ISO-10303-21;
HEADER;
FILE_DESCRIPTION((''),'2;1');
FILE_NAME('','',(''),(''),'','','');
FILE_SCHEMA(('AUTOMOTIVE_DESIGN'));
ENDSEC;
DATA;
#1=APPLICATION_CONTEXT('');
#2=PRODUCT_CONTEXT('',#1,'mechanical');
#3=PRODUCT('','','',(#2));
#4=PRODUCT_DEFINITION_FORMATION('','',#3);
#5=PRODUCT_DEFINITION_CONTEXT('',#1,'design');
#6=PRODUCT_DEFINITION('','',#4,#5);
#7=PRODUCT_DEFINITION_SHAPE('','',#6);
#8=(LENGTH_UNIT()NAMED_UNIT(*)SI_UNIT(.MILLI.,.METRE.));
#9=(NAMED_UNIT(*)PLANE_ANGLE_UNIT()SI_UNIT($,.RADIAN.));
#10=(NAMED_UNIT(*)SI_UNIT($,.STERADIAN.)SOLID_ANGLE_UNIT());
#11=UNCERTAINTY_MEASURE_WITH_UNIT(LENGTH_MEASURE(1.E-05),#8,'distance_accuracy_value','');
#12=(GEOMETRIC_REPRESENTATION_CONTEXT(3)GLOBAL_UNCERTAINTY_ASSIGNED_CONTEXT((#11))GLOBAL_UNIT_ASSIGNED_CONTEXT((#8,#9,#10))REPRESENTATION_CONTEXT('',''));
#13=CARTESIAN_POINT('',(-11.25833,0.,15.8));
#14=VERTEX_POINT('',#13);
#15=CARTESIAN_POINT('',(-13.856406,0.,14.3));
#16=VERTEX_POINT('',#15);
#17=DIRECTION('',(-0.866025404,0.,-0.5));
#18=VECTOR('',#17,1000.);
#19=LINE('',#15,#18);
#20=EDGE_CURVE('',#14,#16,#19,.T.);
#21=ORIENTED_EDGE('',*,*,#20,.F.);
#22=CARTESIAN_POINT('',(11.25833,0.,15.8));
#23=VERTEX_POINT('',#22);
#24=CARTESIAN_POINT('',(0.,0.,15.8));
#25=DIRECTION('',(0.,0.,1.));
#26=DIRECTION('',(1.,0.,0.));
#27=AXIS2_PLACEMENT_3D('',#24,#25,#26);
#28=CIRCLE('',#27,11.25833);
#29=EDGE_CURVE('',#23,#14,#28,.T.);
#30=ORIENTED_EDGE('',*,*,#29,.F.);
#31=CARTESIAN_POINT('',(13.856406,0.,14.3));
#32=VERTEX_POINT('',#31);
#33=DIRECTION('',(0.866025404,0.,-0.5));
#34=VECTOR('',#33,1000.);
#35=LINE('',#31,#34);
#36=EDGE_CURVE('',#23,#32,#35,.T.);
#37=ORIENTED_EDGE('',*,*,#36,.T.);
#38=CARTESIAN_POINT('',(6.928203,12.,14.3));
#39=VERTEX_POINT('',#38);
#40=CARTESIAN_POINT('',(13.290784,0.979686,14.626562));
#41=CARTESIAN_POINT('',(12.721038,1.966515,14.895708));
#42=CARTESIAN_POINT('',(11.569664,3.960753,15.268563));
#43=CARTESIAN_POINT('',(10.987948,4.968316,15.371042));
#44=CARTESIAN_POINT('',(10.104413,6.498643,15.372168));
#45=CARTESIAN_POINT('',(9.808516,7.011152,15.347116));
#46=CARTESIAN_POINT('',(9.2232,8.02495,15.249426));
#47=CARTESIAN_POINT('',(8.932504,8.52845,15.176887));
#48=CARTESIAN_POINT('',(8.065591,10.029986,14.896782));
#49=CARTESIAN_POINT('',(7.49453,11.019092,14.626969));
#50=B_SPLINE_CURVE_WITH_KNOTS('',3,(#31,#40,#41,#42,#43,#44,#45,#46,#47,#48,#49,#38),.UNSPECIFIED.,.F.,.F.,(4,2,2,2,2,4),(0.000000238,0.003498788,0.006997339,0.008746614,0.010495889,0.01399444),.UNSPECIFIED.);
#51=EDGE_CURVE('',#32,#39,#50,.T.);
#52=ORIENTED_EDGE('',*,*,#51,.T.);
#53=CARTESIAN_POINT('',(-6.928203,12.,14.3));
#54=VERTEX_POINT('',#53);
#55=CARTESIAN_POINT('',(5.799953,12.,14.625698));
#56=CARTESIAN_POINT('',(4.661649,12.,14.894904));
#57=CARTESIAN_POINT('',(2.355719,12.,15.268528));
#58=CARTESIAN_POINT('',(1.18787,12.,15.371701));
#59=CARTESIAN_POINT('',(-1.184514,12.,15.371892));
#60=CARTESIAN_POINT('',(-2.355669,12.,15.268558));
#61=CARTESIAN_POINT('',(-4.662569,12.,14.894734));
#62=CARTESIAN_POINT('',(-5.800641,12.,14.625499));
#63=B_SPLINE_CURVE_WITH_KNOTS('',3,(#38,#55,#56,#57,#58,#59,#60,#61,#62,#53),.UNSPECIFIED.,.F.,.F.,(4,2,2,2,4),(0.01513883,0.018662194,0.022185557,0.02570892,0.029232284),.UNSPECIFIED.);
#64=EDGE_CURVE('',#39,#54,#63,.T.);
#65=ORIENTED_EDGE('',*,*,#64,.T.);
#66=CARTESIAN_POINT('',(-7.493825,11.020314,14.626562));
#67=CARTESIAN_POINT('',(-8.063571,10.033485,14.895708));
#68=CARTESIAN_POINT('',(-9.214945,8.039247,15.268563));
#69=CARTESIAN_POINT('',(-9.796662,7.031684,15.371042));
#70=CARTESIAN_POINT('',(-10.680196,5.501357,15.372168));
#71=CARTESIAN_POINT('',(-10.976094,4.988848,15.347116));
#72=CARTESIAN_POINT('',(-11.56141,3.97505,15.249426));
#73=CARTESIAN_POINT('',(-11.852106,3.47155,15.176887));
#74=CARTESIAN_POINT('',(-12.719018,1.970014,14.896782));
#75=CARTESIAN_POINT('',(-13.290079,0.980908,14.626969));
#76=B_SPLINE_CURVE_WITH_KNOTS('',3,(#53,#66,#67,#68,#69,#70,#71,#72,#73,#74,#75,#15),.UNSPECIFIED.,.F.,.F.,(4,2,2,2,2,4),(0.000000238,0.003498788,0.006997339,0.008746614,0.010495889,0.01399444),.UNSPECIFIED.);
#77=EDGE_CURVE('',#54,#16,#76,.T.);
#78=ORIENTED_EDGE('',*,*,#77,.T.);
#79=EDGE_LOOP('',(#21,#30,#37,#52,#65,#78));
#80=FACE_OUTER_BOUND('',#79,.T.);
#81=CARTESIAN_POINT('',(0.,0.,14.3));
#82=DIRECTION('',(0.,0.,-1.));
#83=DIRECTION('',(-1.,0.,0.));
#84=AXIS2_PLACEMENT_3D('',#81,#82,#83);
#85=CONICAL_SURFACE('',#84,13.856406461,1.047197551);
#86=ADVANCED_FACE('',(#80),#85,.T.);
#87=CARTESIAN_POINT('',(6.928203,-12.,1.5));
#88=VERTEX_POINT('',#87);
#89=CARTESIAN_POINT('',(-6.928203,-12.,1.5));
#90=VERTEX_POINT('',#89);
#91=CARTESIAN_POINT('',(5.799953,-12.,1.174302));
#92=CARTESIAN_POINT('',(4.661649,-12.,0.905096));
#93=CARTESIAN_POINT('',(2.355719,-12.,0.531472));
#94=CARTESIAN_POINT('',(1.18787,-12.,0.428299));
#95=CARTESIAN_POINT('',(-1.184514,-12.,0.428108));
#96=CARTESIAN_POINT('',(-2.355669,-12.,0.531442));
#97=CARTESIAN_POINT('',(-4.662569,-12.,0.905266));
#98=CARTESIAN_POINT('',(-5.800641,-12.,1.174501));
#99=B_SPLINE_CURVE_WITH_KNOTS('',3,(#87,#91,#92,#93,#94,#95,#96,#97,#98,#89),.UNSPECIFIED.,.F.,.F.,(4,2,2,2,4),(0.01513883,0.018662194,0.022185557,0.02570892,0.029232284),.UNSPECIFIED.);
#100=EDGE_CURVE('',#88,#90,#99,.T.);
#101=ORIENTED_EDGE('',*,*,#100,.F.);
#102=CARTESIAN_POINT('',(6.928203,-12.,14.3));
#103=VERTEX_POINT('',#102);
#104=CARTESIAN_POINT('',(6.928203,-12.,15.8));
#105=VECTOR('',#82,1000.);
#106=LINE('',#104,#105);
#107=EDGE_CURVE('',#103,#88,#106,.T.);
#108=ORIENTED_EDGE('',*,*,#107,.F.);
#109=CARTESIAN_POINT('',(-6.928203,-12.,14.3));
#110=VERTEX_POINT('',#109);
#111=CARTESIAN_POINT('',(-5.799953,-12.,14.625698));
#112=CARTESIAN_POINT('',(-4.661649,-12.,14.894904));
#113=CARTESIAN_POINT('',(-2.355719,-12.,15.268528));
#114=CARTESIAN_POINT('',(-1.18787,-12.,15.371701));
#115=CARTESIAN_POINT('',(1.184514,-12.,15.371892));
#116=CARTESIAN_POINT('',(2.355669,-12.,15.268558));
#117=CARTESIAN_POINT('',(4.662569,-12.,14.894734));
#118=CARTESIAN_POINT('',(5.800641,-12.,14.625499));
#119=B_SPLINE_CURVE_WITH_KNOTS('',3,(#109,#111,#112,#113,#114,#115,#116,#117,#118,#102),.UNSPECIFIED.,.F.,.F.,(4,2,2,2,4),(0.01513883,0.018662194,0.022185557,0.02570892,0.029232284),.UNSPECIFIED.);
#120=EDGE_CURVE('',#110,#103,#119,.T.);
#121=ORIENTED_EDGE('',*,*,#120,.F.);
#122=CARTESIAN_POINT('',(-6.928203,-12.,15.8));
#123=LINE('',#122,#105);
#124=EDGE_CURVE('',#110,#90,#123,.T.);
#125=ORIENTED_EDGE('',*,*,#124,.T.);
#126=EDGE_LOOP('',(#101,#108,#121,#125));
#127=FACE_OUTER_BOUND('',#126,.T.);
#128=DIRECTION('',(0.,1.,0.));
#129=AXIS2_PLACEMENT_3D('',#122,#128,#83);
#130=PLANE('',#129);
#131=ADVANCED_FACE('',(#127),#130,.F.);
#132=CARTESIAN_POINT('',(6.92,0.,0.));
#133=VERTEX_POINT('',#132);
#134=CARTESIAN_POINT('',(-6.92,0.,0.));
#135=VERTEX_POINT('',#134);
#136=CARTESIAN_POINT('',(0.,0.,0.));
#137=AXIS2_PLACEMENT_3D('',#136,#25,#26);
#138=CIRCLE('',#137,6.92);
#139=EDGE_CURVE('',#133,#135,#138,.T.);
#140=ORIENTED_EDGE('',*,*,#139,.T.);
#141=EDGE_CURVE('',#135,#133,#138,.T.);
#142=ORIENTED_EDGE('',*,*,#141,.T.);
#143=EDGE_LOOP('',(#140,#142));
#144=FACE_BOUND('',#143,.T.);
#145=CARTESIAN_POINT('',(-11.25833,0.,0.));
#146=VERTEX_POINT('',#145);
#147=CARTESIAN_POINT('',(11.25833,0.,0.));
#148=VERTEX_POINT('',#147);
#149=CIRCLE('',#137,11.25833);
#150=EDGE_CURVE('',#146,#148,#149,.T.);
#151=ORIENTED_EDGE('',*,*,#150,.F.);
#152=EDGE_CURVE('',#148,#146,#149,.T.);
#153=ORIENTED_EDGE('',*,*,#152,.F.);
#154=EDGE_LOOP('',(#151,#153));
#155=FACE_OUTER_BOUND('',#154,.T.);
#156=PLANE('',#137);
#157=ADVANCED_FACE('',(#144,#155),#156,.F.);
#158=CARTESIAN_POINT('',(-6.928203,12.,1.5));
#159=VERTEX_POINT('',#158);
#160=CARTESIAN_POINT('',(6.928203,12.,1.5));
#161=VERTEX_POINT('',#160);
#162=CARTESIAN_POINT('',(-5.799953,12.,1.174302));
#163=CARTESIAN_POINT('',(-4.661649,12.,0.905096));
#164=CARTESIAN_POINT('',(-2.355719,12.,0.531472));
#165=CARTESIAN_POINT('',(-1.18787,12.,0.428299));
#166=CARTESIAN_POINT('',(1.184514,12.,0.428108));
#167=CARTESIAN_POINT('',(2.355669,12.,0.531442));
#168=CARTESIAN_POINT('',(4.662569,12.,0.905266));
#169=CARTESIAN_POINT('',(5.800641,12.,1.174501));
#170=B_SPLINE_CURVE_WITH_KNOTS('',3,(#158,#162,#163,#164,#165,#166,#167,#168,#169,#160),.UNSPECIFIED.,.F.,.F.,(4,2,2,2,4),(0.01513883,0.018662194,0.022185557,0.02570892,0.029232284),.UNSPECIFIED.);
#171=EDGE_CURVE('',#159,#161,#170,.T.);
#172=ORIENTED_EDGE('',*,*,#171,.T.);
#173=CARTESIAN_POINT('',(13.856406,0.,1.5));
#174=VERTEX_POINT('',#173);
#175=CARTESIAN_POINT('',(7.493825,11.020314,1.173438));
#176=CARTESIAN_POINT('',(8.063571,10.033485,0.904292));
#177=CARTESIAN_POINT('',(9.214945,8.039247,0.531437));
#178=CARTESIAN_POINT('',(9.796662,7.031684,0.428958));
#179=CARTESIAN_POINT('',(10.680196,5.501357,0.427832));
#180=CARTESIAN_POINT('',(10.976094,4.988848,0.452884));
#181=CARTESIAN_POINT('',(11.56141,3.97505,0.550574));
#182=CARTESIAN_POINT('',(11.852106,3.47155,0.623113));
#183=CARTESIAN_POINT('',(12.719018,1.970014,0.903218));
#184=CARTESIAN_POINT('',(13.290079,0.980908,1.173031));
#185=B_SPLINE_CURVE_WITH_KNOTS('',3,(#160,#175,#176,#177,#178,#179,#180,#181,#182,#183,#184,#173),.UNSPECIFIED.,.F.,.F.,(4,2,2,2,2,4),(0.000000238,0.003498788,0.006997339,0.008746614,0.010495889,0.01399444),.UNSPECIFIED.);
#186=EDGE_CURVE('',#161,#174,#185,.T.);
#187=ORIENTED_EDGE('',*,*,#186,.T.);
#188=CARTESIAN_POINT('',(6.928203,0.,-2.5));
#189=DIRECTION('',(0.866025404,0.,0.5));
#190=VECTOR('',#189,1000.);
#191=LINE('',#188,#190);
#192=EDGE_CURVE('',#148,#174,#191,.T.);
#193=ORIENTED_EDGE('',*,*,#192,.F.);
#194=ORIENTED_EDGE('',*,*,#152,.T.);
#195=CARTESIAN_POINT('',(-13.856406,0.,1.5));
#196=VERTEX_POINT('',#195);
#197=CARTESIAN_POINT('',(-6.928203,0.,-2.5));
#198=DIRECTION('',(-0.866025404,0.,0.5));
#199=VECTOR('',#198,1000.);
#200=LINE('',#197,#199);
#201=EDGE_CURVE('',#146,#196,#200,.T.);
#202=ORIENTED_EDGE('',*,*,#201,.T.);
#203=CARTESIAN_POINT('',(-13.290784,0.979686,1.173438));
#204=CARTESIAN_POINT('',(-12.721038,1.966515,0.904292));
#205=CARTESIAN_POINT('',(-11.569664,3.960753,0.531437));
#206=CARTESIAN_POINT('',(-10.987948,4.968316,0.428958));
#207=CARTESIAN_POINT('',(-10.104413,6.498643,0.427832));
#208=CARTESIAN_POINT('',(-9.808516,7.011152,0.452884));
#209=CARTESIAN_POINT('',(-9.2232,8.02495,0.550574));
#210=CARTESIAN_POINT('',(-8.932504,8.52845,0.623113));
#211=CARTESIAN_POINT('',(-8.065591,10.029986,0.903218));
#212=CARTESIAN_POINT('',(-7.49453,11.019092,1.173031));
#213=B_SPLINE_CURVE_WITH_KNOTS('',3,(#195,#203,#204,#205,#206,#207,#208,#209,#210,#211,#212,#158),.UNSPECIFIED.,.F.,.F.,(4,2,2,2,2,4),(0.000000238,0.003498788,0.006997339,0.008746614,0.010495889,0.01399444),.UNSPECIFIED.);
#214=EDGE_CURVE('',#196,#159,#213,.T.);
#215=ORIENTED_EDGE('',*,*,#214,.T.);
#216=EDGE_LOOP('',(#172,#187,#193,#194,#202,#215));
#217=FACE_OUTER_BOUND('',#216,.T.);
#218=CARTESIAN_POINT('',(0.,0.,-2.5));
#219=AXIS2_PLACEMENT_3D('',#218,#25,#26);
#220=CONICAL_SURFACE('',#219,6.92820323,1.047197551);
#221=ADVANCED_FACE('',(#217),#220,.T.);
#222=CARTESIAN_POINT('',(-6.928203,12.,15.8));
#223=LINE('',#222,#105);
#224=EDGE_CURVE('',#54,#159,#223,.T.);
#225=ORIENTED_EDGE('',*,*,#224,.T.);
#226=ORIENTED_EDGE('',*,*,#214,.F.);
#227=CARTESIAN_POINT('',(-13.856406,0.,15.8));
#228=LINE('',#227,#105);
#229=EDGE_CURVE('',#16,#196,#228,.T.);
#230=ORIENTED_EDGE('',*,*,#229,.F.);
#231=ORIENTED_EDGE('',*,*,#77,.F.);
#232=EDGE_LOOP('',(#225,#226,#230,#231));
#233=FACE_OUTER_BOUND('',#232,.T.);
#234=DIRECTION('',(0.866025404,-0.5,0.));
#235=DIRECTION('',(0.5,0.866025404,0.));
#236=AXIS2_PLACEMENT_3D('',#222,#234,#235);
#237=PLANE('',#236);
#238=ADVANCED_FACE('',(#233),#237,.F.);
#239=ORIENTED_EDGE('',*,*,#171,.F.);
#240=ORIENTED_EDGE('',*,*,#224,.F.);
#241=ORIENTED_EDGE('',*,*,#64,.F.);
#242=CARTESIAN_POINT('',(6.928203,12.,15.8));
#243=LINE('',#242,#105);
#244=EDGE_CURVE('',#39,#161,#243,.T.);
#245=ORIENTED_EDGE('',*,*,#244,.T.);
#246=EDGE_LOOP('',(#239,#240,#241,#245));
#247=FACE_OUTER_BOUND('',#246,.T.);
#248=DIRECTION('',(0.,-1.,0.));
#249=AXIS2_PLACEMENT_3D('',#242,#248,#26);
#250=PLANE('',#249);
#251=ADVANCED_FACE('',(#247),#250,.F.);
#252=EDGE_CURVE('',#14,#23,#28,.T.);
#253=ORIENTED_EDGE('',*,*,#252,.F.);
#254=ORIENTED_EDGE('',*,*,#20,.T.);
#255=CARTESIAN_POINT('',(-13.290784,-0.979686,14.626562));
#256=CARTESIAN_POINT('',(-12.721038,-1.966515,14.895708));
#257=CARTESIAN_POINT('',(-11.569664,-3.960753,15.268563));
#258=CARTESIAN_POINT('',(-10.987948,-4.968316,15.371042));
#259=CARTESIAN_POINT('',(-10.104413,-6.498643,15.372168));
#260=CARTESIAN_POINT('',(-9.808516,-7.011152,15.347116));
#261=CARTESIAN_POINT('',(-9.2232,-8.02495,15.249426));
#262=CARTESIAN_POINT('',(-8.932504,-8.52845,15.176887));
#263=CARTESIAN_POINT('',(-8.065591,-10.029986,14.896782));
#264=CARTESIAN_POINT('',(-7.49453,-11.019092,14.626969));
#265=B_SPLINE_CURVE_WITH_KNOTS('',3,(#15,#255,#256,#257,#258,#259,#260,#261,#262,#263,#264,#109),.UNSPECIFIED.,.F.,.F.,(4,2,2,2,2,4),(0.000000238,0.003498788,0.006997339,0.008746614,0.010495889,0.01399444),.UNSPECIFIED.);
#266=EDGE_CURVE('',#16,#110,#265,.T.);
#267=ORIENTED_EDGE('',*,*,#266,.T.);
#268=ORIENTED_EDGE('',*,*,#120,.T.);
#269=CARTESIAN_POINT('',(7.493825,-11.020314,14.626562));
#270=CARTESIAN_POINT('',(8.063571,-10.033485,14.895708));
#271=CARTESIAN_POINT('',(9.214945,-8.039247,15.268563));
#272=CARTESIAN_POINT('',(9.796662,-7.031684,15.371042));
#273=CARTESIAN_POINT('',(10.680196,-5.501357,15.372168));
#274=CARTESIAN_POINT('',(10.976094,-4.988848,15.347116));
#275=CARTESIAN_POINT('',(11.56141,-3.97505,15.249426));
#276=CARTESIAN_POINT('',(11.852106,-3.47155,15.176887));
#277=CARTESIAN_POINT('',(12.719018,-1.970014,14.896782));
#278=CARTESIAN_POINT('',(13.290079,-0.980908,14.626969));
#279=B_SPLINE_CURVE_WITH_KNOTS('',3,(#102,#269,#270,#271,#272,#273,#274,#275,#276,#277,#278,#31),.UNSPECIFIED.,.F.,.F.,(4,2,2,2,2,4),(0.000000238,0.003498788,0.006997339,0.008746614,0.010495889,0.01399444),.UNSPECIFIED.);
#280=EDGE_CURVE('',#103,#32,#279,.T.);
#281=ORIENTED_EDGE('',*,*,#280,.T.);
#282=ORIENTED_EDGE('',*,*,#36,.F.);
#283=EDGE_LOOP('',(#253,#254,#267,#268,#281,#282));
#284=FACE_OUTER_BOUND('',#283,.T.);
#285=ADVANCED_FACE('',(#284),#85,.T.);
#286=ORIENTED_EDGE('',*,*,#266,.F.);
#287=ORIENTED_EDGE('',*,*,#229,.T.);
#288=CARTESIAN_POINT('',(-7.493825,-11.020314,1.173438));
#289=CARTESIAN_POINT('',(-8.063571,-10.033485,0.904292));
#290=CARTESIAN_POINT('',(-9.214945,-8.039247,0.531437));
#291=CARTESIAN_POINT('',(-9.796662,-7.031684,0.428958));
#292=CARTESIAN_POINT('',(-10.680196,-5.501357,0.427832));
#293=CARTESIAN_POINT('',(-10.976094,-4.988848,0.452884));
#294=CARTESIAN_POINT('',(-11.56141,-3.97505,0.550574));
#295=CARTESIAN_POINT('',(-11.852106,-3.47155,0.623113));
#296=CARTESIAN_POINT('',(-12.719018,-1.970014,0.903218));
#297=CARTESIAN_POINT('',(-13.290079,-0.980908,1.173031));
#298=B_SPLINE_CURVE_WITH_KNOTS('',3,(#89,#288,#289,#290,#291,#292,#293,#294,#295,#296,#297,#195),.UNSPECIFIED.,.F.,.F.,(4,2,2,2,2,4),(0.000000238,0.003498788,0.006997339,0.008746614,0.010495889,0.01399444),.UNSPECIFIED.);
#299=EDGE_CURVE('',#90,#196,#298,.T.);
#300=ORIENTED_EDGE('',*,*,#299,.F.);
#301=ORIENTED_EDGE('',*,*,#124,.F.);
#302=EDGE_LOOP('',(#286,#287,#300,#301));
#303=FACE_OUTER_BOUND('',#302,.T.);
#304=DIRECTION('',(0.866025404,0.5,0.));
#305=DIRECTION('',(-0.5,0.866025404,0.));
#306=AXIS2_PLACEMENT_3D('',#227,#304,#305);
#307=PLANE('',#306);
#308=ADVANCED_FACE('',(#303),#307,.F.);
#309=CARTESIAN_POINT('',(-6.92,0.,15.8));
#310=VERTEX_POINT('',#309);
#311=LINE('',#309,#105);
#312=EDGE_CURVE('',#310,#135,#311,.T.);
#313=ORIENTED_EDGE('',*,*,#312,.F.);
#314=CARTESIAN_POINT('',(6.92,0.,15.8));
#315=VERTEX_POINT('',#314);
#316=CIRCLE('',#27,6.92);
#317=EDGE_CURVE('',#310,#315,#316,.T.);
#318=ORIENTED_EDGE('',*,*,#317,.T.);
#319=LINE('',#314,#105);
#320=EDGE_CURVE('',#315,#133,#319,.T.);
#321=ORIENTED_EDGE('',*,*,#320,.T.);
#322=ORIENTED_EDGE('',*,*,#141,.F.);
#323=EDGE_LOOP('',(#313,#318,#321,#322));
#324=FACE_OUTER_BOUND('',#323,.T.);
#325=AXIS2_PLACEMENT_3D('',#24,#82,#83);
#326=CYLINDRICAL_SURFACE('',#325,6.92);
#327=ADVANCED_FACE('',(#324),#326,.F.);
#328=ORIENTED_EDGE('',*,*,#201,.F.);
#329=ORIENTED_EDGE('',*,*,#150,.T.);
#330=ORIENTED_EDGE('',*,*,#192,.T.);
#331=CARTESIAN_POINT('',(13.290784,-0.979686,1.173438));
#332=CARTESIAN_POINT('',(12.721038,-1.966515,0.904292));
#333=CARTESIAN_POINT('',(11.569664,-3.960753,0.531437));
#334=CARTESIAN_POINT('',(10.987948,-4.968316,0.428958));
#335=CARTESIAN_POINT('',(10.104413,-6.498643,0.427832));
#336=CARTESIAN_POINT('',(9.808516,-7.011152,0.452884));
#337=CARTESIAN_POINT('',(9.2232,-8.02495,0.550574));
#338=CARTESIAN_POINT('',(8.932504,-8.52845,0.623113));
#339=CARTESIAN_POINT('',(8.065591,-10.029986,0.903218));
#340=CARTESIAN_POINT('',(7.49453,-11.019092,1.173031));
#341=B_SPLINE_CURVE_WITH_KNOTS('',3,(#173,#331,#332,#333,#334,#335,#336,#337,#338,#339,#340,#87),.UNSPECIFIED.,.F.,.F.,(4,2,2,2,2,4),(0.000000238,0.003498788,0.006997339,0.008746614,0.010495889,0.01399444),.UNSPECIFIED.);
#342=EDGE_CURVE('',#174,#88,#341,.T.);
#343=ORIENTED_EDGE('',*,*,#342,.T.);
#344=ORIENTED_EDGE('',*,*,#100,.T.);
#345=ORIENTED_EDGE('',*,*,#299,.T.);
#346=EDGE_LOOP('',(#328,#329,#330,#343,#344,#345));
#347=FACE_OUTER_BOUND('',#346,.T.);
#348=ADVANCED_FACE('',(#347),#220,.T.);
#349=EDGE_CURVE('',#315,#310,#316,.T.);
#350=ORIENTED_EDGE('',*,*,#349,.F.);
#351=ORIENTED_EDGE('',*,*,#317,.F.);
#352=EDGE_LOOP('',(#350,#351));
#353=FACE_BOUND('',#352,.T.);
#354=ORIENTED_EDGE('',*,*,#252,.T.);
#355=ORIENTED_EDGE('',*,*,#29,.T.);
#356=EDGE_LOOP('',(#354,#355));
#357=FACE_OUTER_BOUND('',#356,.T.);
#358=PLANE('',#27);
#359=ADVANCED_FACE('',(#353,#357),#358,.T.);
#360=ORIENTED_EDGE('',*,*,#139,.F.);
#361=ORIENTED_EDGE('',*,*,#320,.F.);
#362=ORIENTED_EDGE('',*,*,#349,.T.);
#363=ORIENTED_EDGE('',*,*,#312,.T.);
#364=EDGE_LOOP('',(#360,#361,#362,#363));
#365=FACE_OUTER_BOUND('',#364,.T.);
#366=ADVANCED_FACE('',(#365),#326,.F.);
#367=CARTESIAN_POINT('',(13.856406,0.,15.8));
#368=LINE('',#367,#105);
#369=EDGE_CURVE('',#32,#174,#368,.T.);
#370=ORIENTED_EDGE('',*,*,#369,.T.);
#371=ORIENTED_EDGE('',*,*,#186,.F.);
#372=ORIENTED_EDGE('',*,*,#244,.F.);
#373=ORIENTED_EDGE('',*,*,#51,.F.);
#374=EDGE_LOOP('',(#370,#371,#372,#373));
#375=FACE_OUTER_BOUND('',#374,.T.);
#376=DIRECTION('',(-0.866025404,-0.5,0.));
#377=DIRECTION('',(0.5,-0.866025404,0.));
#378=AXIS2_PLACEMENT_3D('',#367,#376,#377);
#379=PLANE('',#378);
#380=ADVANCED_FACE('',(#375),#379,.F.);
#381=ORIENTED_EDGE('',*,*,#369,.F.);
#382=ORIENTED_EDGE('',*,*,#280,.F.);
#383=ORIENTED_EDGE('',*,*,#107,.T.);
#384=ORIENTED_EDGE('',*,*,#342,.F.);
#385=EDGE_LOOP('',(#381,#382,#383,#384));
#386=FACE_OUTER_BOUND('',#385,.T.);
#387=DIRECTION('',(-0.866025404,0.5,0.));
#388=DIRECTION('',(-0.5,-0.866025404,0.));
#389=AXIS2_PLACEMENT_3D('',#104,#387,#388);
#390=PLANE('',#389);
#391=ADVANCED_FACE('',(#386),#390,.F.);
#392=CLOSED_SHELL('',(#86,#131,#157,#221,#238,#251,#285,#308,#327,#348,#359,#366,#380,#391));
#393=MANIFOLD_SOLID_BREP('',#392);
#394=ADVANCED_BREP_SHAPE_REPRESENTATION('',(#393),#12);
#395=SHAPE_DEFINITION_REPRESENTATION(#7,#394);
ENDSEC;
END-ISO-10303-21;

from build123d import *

# Parameters (mm, degrees)
BOSS_EXTRUDE1_DEPTH = 15.8
SKETCH3_R           = 6.92
CUT_EXTRUDE1_DEPTH  = 25.2


with BuildPart() as part:
    # Sketch1 → Boss-Extrude1 (new body)
    with BuildSketch(Plane.XY):
        Polygon((13.856406461, 0), (6.92820323, 12), (-6.92820323, 12), (-13.856406461, 0), (-6.92820323, -12), (6.92820323, -12), align=None)
    extrude(amount=BOSS_EXTRUDE1_DEPTH)

    # Sketch2 → Cut-Revolve1 (revolve, cut)
    with BuildSketch(Plane(origin=(0, 0, 0), x_dir=(1, 0, 0), z_dir=(0, 1, 0))):
        Polygon((13.856406461, -1.5), (6.92820323, 2.5), (16.856406461, 3.696152423), align=None)
        Polygon((13.856406461, -14.3), (6.92820323, -18.3), (16.856406461, -19.496152423), align=None)
    revolve(axis=Axis((0, 0, 0), (0, 0, 1)), mode=Mode.SUBTRACT)

    # Sketch3 → Cut-Extrude1 (cut, through all)
    with BuildSketch(Plane.XY):
        Circle(SKETCH3_R)
    extrude(amount=CUT_EXTRUDE1_DEPTH, mode=Mode.SUBTRACT)


solid = part.part
